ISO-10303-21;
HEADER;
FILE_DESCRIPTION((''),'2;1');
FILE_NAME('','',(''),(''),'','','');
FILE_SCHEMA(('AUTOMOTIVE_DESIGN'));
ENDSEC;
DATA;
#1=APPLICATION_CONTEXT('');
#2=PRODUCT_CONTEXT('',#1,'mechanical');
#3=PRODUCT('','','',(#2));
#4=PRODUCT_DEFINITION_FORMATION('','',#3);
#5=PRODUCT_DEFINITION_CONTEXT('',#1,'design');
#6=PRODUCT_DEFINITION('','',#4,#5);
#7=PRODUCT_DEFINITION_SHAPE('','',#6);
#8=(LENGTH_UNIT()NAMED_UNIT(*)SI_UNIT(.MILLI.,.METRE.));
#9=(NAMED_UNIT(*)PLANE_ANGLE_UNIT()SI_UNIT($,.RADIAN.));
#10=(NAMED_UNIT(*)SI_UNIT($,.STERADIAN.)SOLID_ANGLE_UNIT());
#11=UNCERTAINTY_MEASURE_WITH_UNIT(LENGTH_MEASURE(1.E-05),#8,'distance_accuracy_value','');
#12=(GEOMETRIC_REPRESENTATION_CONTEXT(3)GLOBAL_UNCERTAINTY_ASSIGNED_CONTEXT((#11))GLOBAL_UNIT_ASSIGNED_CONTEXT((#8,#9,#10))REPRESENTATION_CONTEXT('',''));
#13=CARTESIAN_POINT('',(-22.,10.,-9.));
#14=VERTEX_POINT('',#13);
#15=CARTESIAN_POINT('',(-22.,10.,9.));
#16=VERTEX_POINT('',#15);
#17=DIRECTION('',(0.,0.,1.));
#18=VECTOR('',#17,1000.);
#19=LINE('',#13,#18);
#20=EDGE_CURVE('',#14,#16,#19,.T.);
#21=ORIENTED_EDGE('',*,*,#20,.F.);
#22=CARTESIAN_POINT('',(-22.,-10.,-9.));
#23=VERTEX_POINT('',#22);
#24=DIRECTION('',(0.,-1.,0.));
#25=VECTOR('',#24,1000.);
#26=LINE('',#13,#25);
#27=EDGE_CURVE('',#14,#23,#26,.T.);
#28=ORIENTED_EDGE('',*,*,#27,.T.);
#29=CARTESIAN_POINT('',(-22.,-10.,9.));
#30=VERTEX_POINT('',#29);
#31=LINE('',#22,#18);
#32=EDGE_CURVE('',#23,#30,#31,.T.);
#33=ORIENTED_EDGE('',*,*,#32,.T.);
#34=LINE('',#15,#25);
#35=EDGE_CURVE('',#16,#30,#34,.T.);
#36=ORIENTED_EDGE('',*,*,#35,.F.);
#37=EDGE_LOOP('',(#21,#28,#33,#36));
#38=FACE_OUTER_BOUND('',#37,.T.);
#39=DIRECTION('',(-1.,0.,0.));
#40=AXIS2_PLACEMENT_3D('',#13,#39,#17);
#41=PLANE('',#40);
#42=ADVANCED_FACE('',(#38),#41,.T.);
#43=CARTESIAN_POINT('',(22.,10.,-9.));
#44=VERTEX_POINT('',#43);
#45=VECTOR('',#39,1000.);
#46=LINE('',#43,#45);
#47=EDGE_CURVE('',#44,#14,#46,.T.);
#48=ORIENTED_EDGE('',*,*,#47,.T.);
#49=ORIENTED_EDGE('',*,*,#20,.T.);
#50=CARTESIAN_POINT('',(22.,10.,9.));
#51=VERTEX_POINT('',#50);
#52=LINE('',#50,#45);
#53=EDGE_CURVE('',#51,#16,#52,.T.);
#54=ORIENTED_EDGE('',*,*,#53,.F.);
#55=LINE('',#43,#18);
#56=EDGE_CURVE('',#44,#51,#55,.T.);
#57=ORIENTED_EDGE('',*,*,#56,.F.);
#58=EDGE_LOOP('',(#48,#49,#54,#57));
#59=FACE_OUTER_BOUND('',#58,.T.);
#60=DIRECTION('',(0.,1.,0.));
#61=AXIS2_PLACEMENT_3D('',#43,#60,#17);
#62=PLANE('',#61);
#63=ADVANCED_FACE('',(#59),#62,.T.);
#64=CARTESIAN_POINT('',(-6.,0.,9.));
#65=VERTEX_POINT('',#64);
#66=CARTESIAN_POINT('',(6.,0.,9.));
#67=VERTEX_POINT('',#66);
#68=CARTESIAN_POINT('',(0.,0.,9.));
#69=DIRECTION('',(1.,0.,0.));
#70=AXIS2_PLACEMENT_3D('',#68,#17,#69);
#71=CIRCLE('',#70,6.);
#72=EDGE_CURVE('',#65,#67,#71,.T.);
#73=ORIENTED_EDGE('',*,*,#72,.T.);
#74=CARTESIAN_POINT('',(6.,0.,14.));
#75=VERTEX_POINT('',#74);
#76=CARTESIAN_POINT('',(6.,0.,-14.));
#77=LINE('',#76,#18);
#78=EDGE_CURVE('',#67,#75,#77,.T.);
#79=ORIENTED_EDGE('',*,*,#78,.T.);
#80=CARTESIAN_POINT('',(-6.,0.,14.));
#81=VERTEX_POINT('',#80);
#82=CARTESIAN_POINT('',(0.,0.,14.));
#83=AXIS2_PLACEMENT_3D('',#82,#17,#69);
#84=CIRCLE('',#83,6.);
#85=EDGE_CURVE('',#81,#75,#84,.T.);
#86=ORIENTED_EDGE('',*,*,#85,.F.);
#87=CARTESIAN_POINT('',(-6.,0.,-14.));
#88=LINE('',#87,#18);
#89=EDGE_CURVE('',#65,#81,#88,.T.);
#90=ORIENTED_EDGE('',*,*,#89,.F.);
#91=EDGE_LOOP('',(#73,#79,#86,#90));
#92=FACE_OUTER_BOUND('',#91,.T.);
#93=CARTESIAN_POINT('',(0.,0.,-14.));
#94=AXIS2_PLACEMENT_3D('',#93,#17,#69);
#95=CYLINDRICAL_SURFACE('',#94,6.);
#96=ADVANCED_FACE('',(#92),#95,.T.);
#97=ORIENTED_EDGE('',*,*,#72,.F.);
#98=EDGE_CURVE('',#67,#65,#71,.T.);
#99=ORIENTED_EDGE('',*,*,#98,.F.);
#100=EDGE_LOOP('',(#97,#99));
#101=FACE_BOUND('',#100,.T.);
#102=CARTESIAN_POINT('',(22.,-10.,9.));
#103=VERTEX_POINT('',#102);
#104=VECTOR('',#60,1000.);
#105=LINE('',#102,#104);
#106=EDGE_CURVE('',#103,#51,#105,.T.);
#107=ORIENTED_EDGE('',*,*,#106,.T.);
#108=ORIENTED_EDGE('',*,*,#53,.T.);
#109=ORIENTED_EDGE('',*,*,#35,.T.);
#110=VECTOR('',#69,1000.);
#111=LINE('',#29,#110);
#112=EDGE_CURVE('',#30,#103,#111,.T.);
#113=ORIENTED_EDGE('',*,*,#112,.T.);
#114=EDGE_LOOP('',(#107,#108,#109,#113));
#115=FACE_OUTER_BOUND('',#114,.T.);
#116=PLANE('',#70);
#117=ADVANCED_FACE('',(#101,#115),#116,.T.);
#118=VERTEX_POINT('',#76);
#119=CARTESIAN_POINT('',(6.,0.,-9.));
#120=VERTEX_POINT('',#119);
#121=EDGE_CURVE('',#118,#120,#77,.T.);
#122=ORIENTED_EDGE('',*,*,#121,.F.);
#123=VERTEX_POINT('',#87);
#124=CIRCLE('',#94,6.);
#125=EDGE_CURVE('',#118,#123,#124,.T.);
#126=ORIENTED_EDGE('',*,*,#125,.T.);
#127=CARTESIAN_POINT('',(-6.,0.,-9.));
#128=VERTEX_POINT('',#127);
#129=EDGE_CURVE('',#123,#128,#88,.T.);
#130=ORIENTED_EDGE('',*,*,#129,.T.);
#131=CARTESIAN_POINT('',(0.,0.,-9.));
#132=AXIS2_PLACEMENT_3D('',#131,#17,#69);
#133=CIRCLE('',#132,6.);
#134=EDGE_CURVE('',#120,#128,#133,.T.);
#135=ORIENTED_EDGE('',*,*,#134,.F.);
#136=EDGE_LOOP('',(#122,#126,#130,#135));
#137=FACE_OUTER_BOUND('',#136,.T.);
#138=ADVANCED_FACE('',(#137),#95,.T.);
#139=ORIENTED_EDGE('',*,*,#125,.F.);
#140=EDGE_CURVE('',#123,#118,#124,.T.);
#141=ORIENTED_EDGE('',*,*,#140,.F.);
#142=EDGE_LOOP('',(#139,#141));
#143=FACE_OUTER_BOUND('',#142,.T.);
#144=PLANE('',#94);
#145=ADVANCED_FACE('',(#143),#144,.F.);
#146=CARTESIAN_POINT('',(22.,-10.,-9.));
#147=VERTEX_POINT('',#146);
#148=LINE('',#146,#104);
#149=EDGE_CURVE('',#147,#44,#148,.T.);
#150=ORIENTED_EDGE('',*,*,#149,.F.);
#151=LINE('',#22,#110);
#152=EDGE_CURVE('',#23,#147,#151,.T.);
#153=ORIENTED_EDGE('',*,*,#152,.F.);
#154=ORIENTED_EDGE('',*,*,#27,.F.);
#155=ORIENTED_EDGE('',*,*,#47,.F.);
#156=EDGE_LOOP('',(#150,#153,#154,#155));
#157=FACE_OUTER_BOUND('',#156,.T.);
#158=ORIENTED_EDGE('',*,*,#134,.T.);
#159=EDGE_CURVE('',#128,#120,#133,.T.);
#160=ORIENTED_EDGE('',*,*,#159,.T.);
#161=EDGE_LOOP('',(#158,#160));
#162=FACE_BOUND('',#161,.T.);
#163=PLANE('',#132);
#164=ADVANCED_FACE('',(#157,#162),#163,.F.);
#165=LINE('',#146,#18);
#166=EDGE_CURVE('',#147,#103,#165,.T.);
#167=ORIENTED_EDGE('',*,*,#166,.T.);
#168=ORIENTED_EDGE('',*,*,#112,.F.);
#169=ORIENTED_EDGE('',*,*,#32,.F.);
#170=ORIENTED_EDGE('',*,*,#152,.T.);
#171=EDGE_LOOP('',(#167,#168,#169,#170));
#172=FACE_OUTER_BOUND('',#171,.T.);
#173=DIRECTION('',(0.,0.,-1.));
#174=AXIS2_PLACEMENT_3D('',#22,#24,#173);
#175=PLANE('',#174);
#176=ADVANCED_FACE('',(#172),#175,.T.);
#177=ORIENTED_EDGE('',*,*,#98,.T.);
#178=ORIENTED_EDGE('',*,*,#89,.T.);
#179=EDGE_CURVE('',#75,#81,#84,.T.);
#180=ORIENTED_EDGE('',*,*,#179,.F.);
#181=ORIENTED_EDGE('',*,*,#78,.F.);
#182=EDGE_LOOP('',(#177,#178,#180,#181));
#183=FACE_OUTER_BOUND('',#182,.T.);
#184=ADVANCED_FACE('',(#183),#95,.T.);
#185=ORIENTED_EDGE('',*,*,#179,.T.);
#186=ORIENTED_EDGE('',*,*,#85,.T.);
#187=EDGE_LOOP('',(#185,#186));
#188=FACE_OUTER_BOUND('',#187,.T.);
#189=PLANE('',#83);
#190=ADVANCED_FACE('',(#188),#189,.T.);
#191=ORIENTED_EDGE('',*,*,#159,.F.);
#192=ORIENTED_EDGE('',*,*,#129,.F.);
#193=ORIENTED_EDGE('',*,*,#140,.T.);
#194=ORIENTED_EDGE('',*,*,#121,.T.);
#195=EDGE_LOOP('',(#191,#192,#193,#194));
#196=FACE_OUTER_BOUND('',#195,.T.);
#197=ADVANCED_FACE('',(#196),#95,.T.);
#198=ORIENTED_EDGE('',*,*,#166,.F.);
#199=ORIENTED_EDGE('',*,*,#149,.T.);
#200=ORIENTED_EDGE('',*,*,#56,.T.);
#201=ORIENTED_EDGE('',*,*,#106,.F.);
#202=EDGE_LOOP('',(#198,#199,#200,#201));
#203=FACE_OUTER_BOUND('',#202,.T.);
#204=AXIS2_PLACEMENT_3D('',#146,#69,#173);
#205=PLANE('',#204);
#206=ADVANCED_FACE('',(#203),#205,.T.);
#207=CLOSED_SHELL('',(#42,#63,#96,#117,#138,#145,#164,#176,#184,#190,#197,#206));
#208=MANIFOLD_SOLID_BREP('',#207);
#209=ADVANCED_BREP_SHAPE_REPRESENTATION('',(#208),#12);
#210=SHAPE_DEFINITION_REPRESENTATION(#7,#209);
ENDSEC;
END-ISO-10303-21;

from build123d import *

# Parameters (mm, degrees)
SKETCH_1_W      = 44
SKETCH_1_H      = 20
EXTRUDE_1_DEPTH = 9
SKETCH_2_R      = 6
EXTRUDE_2_DEPTH = 14


with BuildPart() as part:
    # 草图1 → 凸台-拉伸1 (new, symmetric)
    with BuildSketch(Plane.XY):
        Rectangle(SKETCH_1_W, SKETCH_1_H)
    extrude(amount=EXTRUDE_1_DEPTH, both=True)

    # 草图2 → 凸台-拉伸2 (add, symmetric)
    with BuildSketch(Plane.XY):
        Circle(SKETCH_2_R)
    extrude(amount=EXTRUDE_2_DEPTH, both=True)


solid = part.part
